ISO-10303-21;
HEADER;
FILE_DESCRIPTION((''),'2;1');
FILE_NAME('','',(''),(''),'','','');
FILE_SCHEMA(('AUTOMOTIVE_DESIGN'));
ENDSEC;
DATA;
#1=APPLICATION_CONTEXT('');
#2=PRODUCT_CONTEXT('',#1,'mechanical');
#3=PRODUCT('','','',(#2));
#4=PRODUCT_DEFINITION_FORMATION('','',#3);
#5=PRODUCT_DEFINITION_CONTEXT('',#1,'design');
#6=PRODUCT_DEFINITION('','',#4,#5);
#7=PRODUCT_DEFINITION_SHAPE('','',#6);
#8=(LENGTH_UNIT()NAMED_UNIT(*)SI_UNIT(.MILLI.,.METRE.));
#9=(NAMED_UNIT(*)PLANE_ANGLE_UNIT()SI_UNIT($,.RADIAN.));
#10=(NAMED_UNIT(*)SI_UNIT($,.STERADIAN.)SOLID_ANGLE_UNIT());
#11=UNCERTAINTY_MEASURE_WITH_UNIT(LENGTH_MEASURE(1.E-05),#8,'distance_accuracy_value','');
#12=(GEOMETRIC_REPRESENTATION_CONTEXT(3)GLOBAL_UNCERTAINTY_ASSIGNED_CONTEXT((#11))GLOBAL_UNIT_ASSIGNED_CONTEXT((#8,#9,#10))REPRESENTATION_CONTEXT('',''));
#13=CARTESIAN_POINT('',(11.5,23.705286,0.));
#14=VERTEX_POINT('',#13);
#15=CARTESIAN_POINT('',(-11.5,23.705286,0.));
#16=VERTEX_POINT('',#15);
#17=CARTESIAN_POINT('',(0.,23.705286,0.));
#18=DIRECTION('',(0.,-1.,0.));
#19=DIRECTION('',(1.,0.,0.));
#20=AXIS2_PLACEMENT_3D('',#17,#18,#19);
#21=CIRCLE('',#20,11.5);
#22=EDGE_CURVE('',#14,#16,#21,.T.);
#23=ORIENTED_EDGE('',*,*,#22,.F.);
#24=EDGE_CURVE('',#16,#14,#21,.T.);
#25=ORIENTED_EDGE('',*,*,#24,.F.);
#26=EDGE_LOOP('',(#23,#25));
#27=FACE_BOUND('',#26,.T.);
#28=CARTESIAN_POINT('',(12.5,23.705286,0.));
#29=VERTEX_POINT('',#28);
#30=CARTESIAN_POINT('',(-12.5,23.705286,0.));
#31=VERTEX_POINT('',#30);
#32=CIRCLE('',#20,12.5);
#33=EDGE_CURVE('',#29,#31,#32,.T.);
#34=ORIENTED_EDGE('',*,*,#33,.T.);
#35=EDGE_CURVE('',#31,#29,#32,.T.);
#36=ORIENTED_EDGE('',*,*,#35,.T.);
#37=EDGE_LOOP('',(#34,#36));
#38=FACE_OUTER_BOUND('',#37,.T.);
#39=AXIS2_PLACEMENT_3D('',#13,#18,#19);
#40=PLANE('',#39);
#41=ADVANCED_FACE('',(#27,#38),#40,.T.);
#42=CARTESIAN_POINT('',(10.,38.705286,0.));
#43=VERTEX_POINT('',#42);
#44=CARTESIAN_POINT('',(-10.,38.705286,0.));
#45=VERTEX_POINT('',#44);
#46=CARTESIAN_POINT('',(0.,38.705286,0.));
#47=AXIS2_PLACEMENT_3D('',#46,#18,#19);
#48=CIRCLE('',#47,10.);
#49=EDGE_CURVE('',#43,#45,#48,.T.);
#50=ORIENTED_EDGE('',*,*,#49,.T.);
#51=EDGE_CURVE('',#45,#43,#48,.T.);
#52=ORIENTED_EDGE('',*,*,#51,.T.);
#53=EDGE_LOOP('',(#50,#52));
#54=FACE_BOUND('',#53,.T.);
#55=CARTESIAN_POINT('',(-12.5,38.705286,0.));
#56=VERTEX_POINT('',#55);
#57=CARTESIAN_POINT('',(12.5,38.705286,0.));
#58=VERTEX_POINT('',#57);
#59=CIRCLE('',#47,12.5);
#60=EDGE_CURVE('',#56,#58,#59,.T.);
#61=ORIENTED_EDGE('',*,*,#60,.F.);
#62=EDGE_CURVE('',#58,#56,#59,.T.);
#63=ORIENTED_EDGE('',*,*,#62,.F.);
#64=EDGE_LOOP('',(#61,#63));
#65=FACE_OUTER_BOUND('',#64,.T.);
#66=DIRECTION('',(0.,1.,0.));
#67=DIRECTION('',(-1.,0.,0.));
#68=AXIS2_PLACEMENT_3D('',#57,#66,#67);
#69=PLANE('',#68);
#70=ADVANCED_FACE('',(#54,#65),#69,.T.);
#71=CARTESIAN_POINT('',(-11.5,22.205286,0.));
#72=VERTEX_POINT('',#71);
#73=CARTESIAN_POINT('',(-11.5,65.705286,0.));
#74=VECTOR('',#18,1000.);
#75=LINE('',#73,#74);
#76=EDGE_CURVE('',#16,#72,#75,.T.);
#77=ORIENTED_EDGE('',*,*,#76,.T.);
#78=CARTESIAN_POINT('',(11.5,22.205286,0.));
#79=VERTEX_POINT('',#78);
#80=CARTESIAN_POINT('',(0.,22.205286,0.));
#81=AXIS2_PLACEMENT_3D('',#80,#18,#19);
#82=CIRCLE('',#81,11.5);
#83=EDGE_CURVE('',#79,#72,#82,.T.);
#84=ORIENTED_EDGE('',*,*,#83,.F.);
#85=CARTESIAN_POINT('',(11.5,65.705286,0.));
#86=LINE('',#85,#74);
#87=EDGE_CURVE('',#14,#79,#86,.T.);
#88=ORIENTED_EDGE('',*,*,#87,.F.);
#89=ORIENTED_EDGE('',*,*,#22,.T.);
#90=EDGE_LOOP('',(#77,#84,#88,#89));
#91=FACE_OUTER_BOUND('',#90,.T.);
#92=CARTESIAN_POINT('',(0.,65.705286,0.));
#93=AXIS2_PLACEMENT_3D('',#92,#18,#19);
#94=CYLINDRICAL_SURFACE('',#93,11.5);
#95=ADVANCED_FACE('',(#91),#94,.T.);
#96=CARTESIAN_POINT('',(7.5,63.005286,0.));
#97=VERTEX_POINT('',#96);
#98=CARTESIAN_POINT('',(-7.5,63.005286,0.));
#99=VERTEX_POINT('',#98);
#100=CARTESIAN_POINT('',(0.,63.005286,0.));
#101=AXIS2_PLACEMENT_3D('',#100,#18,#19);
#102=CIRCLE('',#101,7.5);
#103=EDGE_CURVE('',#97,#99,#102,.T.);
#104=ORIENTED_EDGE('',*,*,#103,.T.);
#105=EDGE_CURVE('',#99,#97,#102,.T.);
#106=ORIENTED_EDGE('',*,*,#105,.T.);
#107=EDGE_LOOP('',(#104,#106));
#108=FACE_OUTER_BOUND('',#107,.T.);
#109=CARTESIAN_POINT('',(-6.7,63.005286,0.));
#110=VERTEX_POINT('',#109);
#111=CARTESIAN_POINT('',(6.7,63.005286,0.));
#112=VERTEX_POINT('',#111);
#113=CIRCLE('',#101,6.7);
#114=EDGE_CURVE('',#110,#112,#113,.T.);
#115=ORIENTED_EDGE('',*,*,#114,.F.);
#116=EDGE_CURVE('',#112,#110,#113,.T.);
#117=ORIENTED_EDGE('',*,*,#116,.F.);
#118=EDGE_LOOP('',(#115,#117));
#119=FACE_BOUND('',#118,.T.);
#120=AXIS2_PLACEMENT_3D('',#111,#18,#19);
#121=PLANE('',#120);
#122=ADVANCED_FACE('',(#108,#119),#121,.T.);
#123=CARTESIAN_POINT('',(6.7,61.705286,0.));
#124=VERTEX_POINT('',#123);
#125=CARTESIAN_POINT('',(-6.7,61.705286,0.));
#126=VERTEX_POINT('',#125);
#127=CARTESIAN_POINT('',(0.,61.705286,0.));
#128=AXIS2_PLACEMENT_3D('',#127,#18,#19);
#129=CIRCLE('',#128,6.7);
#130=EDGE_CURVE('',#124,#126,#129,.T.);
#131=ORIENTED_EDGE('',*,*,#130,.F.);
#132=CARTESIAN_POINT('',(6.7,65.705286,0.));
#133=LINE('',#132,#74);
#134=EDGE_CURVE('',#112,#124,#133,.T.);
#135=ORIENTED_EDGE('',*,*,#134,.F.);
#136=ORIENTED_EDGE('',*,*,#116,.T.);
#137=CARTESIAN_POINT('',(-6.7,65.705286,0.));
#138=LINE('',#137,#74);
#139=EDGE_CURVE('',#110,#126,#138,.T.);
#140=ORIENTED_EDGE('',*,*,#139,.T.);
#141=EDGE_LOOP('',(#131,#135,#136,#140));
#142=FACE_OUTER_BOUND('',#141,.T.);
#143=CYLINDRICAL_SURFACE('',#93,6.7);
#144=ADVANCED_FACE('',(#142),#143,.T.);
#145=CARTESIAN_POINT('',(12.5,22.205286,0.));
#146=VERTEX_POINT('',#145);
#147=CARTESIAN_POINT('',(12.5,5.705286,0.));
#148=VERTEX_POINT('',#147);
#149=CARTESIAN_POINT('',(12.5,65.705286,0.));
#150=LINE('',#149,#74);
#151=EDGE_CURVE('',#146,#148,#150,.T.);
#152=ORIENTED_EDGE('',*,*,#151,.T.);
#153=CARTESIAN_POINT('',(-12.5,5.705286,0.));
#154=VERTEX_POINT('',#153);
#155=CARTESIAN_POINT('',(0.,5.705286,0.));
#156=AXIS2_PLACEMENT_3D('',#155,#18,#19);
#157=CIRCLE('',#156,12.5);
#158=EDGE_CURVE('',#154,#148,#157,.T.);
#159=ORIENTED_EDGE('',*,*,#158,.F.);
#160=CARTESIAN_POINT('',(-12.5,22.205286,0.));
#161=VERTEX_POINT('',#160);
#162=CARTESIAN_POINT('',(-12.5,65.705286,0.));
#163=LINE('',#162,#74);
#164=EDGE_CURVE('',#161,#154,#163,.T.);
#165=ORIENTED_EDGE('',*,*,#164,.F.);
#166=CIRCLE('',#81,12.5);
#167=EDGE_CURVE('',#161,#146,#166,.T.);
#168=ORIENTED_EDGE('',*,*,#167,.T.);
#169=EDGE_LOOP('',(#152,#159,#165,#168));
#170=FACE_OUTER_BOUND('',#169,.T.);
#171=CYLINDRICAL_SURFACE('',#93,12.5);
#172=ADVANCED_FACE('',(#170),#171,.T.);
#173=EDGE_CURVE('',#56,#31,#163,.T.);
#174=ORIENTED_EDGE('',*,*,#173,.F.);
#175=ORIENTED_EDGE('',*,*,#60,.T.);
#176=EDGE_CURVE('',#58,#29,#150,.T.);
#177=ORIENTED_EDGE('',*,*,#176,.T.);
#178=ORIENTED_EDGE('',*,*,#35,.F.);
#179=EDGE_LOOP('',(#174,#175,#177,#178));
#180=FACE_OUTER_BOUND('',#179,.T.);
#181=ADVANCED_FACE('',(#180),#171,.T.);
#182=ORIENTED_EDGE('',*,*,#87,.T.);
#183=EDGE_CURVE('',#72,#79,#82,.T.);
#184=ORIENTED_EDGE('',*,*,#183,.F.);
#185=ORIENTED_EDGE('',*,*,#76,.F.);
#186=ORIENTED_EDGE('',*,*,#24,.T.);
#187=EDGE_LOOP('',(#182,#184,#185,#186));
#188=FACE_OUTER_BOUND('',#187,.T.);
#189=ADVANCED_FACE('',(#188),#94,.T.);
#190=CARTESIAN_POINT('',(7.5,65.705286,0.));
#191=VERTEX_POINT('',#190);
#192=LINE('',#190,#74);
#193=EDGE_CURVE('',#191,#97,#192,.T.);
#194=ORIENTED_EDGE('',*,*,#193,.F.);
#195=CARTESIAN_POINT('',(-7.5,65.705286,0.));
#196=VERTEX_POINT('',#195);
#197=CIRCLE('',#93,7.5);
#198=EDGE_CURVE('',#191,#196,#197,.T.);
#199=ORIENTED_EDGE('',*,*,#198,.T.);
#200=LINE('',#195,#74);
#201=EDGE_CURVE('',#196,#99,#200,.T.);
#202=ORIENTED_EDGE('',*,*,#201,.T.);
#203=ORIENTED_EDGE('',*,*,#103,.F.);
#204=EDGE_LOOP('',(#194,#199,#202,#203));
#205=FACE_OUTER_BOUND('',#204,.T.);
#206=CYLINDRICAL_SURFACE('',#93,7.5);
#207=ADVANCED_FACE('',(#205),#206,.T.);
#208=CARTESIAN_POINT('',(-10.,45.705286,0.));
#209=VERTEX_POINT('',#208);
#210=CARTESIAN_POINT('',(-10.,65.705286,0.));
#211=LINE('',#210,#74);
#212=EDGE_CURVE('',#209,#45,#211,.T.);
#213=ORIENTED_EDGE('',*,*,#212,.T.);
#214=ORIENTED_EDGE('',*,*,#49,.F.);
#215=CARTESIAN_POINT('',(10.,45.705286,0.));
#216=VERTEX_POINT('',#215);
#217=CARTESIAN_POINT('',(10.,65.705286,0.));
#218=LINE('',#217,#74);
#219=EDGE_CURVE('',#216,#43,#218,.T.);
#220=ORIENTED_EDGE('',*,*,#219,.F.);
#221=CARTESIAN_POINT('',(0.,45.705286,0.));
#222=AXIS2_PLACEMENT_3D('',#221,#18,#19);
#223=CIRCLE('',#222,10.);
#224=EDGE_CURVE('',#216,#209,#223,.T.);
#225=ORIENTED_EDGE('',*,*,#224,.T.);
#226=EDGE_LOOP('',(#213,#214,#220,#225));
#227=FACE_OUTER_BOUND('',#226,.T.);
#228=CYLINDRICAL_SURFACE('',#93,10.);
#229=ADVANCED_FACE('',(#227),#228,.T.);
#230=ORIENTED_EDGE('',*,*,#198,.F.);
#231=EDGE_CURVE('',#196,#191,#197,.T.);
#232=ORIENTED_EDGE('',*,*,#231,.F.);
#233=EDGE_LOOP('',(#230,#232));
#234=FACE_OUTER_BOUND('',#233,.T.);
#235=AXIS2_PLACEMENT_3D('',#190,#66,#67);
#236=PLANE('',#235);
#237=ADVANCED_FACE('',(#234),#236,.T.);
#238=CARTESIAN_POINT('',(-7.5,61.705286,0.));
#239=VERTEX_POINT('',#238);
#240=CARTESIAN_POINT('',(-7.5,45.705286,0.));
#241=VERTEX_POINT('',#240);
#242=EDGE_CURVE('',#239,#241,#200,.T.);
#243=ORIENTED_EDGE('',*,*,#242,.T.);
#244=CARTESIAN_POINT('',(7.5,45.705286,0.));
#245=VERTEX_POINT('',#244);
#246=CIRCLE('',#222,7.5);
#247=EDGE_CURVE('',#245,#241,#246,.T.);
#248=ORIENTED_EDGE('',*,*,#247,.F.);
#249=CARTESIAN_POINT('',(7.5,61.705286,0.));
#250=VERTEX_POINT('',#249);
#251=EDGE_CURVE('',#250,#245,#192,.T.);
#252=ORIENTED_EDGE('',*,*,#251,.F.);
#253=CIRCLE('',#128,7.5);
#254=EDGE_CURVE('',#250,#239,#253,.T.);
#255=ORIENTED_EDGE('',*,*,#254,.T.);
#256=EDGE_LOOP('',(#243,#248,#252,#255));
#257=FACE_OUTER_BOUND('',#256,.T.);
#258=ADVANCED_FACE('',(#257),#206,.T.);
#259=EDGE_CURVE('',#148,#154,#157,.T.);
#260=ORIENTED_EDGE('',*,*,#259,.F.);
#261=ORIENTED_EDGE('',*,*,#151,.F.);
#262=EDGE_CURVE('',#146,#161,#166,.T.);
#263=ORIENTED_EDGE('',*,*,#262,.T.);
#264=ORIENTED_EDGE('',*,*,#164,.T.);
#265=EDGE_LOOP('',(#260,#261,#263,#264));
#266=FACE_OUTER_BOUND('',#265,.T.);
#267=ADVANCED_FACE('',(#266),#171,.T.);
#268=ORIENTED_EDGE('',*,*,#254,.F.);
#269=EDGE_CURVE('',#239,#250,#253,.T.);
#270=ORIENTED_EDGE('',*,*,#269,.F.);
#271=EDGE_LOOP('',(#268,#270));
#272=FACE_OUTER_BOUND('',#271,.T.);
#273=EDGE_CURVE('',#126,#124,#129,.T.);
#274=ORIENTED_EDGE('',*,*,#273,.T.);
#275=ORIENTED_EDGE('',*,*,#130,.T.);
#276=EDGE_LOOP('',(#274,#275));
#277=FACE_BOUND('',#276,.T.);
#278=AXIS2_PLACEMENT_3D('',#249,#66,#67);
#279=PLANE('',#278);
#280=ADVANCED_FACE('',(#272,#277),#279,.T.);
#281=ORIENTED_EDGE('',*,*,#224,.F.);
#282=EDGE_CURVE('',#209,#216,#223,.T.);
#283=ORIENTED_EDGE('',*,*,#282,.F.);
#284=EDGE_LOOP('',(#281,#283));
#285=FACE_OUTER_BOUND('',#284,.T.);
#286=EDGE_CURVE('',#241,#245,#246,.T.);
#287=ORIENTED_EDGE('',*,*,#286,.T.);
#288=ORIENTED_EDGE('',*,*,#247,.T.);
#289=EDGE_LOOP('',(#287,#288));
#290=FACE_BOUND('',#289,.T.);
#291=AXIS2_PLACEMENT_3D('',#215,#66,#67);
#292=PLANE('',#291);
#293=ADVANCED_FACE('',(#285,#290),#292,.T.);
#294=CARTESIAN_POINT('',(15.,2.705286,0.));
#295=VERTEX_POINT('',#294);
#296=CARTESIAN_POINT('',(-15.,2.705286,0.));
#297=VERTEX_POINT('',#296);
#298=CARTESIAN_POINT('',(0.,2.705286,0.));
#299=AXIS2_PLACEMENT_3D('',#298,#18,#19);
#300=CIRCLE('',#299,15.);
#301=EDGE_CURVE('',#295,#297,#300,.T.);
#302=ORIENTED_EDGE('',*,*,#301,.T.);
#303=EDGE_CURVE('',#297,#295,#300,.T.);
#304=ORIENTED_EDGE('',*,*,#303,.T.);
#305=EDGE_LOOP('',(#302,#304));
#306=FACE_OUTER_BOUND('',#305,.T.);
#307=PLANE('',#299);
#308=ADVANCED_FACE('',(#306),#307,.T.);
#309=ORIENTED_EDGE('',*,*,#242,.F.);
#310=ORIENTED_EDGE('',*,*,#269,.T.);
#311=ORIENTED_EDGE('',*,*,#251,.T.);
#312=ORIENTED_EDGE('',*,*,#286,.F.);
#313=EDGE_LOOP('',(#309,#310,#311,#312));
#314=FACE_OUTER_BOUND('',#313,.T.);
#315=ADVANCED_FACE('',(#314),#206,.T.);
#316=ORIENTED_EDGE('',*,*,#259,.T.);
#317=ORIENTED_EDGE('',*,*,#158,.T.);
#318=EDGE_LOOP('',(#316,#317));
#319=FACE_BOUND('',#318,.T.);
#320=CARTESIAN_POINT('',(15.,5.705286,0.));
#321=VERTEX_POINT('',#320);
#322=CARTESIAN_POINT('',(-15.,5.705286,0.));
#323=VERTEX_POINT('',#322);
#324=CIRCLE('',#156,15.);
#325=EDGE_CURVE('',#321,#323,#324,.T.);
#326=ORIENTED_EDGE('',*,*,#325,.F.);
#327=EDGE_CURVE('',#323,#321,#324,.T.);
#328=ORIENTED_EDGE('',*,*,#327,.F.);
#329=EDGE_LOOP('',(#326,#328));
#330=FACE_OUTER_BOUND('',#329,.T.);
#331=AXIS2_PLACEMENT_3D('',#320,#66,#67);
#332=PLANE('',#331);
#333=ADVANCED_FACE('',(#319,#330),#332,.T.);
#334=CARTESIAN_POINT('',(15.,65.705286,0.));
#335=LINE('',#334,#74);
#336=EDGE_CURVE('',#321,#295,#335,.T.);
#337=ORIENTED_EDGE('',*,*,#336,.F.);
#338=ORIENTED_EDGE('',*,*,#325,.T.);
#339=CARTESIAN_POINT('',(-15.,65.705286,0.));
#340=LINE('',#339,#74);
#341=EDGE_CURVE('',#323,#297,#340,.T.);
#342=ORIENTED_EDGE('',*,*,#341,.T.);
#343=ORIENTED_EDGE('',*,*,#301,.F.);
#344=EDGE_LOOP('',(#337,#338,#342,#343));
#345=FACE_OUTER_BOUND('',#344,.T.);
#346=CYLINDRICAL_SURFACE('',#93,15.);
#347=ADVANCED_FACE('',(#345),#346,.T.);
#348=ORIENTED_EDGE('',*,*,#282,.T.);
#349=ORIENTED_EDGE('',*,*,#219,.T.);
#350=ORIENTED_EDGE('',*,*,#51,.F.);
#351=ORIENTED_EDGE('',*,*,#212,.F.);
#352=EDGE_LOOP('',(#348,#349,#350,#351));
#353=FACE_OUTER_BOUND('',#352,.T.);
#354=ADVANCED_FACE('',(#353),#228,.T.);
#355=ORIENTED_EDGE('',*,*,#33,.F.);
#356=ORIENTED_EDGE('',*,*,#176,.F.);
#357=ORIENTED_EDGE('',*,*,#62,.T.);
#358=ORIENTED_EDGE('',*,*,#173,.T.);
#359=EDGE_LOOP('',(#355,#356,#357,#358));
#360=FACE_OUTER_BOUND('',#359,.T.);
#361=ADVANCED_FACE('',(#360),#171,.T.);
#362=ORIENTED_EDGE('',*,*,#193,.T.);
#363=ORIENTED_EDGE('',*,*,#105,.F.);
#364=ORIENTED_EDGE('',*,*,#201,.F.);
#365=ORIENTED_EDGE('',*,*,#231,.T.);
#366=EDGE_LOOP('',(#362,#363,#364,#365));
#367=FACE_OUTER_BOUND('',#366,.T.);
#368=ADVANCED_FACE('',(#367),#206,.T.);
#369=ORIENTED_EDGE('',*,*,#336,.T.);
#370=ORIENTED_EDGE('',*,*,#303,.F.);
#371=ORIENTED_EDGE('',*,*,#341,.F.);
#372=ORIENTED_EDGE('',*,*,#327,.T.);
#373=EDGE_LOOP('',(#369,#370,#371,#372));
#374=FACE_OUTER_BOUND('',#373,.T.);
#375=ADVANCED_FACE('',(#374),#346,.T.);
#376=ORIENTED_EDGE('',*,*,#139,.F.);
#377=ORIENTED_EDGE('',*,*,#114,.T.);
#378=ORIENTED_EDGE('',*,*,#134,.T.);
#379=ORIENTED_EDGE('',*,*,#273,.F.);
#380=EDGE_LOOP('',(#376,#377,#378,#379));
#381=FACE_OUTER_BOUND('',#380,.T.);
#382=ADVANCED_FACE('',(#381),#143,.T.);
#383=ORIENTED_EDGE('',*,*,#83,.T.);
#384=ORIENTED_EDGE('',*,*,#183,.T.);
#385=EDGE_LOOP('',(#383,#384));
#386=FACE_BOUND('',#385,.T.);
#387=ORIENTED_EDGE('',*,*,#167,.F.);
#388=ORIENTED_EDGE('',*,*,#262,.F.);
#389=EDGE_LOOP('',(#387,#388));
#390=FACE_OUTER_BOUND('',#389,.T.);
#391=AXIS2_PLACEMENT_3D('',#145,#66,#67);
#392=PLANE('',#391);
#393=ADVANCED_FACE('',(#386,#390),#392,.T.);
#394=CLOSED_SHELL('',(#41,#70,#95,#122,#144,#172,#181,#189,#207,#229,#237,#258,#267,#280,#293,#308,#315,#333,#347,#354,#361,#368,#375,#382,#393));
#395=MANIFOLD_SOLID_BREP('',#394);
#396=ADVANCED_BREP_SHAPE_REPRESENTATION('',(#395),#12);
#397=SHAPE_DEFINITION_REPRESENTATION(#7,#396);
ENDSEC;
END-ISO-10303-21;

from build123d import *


with BuildPart() as part:
    # 草图1 → 旋转1 (revolve)
    with BuildSketch(Plane.XY):
        Polygon((7.5, 65.705286307), (0, 65.705286307), (0, 2.705286307), (15, 2.705286307), (15, 5.705286307), (12.5, 5.705286307), (12.5, 22.205286307), (11.5, 22.205286307), (11.5, 23.705286307), (12.5, 23.705286307), (12.5, 38.705286307), (10, 38.705286307), (10, 45.705286307), (7.5, 45.705286307), (7.5, 61.705286307), (6.7, 61.705286307), (6.7, 63.005286307), (7.5, 63.005286307), align=None)
    revolve(axis=Axis((0, 65.705286307, 0), (0, -1, 0)))


solid = part.part
